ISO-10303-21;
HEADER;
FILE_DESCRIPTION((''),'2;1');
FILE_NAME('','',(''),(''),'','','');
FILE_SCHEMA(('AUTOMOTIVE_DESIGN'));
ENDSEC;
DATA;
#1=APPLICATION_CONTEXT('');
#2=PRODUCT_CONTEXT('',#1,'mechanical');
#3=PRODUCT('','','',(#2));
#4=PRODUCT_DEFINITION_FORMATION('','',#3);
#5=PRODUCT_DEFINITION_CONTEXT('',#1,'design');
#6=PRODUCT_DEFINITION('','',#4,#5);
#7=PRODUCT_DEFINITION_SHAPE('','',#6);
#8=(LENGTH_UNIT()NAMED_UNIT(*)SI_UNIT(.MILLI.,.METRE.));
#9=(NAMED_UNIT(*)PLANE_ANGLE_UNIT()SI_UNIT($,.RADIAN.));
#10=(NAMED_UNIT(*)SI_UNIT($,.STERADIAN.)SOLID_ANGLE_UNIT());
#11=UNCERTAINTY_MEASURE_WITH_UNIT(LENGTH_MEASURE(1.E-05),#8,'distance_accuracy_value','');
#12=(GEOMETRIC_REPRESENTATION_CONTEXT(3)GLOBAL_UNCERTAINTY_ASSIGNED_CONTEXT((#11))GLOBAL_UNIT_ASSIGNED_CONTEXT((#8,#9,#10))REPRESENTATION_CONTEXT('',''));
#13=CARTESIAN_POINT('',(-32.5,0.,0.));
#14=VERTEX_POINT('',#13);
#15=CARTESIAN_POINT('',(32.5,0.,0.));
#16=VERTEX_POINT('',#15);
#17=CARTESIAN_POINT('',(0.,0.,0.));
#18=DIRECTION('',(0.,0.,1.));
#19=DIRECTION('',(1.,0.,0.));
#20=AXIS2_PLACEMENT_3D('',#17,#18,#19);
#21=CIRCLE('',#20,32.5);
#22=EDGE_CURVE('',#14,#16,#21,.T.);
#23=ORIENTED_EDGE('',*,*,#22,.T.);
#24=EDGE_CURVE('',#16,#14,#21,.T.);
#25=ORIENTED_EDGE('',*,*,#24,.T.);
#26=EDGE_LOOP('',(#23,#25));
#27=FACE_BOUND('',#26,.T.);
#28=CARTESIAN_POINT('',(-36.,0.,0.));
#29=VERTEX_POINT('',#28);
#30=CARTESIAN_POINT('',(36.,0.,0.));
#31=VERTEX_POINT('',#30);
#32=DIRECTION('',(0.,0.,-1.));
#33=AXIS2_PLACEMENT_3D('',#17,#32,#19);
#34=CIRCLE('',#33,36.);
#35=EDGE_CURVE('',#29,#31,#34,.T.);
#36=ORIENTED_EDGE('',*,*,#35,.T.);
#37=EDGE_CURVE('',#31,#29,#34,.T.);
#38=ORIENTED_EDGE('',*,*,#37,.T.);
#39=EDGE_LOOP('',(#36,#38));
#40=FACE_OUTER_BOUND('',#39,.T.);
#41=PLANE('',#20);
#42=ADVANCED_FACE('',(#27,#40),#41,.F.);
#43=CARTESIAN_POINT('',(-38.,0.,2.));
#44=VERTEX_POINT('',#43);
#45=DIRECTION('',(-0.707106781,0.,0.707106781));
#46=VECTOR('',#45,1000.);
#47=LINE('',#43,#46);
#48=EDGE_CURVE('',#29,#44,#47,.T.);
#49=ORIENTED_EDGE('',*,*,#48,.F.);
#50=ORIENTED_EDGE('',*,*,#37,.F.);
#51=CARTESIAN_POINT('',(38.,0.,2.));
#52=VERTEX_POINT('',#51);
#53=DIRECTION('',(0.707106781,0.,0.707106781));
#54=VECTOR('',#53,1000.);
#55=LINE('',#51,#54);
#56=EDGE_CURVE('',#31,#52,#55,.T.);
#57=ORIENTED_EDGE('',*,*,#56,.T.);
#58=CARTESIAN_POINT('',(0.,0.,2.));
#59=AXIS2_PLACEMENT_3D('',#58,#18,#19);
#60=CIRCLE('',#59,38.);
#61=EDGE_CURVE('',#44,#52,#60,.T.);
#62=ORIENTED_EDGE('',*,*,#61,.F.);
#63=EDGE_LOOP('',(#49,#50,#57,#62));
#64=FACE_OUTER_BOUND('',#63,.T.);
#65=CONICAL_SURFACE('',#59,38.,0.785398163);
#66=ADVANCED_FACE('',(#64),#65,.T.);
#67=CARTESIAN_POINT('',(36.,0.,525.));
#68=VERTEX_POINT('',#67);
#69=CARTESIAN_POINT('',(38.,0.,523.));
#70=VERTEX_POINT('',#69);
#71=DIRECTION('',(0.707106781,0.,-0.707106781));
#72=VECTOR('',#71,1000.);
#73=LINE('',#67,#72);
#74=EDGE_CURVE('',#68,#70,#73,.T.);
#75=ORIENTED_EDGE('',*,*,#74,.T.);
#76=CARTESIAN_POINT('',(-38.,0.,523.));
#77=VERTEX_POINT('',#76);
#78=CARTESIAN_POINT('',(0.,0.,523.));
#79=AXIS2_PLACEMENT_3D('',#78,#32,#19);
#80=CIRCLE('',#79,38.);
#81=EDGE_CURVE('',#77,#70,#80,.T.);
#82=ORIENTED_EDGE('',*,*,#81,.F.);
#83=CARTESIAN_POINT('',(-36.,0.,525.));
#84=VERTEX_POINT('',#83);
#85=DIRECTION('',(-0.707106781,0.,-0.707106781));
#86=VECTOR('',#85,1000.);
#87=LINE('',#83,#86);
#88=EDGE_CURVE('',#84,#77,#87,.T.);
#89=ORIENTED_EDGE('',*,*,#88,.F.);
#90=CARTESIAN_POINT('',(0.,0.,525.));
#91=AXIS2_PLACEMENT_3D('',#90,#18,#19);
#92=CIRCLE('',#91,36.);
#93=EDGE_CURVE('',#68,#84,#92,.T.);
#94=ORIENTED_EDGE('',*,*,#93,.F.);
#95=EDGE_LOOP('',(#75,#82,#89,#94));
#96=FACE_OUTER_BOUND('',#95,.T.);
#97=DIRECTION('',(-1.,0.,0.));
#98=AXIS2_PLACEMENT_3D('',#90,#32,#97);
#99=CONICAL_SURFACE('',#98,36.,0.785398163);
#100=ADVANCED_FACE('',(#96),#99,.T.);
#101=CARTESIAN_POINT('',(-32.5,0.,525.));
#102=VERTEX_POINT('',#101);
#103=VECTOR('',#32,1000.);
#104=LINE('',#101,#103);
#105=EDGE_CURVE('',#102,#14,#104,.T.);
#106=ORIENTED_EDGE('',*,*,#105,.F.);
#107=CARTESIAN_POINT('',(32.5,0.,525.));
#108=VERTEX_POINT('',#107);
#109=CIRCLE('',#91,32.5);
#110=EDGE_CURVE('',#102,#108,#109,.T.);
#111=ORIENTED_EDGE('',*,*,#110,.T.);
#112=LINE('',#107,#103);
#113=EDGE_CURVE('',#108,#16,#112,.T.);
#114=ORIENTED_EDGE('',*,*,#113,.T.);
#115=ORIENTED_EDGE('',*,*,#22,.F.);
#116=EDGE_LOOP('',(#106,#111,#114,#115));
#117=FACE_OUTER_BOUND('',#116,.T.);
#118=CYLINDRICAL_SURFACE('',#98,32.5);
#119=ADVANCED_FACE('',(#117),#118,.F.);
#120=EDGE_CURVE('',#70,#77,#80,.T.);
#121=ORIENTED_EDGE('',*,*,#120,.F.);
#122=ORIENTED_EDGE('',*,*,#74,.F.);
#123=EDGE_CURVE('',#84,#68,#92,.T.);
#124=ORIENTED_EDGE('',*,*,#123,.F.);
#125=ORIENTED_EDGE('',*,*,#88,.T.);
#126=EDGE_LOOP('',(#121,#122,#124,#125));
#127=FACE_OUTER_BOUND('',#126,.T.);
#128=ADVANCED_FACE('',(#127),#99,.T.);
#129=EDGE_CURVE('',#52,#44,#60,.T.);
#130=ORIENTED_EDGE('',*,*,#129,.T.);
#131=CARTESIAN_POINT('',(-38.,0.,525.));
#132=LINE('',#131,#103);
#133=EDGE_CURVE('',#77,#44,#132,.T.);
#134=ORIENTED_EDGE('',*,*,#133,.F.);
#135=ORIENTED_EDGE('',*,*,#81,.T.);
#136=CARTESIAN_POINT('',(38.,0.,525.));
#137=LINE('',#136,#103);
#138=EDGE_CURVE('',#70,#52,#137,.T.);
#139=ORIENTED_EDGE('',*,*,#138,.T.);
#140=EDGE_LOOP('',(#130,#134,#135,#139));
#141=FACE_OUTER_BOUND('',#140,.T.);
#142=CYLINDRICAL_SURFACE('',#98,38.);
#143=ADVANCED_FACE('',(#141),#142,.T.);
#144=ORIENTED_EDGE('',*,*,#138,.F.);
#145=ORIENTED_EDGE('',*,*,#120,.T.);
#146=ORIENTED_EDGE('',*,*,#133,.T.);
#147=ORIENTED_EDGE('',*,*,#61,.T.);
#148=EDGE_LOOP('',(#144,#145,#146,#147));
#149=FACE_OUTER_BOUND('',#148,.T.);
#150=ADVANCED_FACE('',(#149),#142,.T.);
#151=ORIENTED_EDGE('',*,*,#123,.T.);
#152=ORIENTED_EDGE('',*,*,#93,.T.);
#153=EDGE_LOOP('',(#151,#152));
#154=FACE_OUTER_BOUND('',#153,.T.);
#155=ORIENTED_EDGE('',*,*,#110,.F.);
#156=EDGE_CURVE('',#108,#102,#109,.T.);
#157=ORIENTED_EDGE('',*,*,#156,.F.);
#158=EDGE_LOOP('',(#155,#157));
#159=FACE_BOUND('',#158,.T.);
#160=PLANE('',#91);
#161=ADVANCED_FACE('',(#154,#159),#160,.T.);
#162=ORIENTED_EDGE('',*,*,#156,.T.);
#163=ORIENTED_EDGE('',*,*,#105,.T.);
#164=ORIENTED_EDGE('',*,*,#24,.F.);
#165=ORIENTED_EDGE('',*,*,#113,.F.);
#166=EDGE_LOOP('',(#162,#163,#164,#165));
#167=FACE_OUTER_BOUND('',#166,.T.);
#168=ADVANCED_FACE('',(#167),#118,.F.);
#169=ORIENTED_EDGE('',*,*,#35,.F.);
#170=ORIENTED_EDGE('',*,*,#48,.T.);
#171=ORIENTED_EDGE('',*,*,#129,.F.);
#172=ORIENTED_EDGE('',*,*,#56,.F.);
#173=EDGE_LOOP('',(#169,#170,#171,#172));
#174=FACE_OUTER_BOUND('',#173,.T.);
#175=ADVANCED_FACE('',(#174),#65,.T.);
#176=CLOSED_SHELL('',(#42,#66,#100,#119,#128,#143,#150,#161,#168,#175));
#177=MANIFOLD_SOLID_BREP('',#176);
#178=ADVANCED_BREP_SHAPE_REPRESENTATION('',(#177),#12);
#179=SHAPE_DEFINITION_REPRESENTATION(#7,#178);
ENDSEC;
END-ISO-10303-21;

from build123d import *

# Parameters (mm, degrees)
SKETCH_1_R      = 38
SKETCH_1_R_2    = 32.5
EXTRUDE_1_DEPTH = 525
CHAMFER_1_SIZE  = 2


with BuildPart() as part:
    # 草图1 → 凸台-拉伸1 (new body)
    with BuildSketch(Plane.XY):
        Circle(SKETCH_1_R)
        Circle(SKETCH_1_R_2, mode=Mode.SUBTRACT)
    extrude(amount=EXTRUDE_1_DEPTH)

    # 倒角1
    chamfer_1_edges = [part.edges().sort_by_distance(p)[0] for p in [
        (-38, 0, 0),
        (-38, 0, 525),
    ]]
    chamfer(chamfer_1_edges, length=CHAMFER_1_SIZE)


solid = part.part
